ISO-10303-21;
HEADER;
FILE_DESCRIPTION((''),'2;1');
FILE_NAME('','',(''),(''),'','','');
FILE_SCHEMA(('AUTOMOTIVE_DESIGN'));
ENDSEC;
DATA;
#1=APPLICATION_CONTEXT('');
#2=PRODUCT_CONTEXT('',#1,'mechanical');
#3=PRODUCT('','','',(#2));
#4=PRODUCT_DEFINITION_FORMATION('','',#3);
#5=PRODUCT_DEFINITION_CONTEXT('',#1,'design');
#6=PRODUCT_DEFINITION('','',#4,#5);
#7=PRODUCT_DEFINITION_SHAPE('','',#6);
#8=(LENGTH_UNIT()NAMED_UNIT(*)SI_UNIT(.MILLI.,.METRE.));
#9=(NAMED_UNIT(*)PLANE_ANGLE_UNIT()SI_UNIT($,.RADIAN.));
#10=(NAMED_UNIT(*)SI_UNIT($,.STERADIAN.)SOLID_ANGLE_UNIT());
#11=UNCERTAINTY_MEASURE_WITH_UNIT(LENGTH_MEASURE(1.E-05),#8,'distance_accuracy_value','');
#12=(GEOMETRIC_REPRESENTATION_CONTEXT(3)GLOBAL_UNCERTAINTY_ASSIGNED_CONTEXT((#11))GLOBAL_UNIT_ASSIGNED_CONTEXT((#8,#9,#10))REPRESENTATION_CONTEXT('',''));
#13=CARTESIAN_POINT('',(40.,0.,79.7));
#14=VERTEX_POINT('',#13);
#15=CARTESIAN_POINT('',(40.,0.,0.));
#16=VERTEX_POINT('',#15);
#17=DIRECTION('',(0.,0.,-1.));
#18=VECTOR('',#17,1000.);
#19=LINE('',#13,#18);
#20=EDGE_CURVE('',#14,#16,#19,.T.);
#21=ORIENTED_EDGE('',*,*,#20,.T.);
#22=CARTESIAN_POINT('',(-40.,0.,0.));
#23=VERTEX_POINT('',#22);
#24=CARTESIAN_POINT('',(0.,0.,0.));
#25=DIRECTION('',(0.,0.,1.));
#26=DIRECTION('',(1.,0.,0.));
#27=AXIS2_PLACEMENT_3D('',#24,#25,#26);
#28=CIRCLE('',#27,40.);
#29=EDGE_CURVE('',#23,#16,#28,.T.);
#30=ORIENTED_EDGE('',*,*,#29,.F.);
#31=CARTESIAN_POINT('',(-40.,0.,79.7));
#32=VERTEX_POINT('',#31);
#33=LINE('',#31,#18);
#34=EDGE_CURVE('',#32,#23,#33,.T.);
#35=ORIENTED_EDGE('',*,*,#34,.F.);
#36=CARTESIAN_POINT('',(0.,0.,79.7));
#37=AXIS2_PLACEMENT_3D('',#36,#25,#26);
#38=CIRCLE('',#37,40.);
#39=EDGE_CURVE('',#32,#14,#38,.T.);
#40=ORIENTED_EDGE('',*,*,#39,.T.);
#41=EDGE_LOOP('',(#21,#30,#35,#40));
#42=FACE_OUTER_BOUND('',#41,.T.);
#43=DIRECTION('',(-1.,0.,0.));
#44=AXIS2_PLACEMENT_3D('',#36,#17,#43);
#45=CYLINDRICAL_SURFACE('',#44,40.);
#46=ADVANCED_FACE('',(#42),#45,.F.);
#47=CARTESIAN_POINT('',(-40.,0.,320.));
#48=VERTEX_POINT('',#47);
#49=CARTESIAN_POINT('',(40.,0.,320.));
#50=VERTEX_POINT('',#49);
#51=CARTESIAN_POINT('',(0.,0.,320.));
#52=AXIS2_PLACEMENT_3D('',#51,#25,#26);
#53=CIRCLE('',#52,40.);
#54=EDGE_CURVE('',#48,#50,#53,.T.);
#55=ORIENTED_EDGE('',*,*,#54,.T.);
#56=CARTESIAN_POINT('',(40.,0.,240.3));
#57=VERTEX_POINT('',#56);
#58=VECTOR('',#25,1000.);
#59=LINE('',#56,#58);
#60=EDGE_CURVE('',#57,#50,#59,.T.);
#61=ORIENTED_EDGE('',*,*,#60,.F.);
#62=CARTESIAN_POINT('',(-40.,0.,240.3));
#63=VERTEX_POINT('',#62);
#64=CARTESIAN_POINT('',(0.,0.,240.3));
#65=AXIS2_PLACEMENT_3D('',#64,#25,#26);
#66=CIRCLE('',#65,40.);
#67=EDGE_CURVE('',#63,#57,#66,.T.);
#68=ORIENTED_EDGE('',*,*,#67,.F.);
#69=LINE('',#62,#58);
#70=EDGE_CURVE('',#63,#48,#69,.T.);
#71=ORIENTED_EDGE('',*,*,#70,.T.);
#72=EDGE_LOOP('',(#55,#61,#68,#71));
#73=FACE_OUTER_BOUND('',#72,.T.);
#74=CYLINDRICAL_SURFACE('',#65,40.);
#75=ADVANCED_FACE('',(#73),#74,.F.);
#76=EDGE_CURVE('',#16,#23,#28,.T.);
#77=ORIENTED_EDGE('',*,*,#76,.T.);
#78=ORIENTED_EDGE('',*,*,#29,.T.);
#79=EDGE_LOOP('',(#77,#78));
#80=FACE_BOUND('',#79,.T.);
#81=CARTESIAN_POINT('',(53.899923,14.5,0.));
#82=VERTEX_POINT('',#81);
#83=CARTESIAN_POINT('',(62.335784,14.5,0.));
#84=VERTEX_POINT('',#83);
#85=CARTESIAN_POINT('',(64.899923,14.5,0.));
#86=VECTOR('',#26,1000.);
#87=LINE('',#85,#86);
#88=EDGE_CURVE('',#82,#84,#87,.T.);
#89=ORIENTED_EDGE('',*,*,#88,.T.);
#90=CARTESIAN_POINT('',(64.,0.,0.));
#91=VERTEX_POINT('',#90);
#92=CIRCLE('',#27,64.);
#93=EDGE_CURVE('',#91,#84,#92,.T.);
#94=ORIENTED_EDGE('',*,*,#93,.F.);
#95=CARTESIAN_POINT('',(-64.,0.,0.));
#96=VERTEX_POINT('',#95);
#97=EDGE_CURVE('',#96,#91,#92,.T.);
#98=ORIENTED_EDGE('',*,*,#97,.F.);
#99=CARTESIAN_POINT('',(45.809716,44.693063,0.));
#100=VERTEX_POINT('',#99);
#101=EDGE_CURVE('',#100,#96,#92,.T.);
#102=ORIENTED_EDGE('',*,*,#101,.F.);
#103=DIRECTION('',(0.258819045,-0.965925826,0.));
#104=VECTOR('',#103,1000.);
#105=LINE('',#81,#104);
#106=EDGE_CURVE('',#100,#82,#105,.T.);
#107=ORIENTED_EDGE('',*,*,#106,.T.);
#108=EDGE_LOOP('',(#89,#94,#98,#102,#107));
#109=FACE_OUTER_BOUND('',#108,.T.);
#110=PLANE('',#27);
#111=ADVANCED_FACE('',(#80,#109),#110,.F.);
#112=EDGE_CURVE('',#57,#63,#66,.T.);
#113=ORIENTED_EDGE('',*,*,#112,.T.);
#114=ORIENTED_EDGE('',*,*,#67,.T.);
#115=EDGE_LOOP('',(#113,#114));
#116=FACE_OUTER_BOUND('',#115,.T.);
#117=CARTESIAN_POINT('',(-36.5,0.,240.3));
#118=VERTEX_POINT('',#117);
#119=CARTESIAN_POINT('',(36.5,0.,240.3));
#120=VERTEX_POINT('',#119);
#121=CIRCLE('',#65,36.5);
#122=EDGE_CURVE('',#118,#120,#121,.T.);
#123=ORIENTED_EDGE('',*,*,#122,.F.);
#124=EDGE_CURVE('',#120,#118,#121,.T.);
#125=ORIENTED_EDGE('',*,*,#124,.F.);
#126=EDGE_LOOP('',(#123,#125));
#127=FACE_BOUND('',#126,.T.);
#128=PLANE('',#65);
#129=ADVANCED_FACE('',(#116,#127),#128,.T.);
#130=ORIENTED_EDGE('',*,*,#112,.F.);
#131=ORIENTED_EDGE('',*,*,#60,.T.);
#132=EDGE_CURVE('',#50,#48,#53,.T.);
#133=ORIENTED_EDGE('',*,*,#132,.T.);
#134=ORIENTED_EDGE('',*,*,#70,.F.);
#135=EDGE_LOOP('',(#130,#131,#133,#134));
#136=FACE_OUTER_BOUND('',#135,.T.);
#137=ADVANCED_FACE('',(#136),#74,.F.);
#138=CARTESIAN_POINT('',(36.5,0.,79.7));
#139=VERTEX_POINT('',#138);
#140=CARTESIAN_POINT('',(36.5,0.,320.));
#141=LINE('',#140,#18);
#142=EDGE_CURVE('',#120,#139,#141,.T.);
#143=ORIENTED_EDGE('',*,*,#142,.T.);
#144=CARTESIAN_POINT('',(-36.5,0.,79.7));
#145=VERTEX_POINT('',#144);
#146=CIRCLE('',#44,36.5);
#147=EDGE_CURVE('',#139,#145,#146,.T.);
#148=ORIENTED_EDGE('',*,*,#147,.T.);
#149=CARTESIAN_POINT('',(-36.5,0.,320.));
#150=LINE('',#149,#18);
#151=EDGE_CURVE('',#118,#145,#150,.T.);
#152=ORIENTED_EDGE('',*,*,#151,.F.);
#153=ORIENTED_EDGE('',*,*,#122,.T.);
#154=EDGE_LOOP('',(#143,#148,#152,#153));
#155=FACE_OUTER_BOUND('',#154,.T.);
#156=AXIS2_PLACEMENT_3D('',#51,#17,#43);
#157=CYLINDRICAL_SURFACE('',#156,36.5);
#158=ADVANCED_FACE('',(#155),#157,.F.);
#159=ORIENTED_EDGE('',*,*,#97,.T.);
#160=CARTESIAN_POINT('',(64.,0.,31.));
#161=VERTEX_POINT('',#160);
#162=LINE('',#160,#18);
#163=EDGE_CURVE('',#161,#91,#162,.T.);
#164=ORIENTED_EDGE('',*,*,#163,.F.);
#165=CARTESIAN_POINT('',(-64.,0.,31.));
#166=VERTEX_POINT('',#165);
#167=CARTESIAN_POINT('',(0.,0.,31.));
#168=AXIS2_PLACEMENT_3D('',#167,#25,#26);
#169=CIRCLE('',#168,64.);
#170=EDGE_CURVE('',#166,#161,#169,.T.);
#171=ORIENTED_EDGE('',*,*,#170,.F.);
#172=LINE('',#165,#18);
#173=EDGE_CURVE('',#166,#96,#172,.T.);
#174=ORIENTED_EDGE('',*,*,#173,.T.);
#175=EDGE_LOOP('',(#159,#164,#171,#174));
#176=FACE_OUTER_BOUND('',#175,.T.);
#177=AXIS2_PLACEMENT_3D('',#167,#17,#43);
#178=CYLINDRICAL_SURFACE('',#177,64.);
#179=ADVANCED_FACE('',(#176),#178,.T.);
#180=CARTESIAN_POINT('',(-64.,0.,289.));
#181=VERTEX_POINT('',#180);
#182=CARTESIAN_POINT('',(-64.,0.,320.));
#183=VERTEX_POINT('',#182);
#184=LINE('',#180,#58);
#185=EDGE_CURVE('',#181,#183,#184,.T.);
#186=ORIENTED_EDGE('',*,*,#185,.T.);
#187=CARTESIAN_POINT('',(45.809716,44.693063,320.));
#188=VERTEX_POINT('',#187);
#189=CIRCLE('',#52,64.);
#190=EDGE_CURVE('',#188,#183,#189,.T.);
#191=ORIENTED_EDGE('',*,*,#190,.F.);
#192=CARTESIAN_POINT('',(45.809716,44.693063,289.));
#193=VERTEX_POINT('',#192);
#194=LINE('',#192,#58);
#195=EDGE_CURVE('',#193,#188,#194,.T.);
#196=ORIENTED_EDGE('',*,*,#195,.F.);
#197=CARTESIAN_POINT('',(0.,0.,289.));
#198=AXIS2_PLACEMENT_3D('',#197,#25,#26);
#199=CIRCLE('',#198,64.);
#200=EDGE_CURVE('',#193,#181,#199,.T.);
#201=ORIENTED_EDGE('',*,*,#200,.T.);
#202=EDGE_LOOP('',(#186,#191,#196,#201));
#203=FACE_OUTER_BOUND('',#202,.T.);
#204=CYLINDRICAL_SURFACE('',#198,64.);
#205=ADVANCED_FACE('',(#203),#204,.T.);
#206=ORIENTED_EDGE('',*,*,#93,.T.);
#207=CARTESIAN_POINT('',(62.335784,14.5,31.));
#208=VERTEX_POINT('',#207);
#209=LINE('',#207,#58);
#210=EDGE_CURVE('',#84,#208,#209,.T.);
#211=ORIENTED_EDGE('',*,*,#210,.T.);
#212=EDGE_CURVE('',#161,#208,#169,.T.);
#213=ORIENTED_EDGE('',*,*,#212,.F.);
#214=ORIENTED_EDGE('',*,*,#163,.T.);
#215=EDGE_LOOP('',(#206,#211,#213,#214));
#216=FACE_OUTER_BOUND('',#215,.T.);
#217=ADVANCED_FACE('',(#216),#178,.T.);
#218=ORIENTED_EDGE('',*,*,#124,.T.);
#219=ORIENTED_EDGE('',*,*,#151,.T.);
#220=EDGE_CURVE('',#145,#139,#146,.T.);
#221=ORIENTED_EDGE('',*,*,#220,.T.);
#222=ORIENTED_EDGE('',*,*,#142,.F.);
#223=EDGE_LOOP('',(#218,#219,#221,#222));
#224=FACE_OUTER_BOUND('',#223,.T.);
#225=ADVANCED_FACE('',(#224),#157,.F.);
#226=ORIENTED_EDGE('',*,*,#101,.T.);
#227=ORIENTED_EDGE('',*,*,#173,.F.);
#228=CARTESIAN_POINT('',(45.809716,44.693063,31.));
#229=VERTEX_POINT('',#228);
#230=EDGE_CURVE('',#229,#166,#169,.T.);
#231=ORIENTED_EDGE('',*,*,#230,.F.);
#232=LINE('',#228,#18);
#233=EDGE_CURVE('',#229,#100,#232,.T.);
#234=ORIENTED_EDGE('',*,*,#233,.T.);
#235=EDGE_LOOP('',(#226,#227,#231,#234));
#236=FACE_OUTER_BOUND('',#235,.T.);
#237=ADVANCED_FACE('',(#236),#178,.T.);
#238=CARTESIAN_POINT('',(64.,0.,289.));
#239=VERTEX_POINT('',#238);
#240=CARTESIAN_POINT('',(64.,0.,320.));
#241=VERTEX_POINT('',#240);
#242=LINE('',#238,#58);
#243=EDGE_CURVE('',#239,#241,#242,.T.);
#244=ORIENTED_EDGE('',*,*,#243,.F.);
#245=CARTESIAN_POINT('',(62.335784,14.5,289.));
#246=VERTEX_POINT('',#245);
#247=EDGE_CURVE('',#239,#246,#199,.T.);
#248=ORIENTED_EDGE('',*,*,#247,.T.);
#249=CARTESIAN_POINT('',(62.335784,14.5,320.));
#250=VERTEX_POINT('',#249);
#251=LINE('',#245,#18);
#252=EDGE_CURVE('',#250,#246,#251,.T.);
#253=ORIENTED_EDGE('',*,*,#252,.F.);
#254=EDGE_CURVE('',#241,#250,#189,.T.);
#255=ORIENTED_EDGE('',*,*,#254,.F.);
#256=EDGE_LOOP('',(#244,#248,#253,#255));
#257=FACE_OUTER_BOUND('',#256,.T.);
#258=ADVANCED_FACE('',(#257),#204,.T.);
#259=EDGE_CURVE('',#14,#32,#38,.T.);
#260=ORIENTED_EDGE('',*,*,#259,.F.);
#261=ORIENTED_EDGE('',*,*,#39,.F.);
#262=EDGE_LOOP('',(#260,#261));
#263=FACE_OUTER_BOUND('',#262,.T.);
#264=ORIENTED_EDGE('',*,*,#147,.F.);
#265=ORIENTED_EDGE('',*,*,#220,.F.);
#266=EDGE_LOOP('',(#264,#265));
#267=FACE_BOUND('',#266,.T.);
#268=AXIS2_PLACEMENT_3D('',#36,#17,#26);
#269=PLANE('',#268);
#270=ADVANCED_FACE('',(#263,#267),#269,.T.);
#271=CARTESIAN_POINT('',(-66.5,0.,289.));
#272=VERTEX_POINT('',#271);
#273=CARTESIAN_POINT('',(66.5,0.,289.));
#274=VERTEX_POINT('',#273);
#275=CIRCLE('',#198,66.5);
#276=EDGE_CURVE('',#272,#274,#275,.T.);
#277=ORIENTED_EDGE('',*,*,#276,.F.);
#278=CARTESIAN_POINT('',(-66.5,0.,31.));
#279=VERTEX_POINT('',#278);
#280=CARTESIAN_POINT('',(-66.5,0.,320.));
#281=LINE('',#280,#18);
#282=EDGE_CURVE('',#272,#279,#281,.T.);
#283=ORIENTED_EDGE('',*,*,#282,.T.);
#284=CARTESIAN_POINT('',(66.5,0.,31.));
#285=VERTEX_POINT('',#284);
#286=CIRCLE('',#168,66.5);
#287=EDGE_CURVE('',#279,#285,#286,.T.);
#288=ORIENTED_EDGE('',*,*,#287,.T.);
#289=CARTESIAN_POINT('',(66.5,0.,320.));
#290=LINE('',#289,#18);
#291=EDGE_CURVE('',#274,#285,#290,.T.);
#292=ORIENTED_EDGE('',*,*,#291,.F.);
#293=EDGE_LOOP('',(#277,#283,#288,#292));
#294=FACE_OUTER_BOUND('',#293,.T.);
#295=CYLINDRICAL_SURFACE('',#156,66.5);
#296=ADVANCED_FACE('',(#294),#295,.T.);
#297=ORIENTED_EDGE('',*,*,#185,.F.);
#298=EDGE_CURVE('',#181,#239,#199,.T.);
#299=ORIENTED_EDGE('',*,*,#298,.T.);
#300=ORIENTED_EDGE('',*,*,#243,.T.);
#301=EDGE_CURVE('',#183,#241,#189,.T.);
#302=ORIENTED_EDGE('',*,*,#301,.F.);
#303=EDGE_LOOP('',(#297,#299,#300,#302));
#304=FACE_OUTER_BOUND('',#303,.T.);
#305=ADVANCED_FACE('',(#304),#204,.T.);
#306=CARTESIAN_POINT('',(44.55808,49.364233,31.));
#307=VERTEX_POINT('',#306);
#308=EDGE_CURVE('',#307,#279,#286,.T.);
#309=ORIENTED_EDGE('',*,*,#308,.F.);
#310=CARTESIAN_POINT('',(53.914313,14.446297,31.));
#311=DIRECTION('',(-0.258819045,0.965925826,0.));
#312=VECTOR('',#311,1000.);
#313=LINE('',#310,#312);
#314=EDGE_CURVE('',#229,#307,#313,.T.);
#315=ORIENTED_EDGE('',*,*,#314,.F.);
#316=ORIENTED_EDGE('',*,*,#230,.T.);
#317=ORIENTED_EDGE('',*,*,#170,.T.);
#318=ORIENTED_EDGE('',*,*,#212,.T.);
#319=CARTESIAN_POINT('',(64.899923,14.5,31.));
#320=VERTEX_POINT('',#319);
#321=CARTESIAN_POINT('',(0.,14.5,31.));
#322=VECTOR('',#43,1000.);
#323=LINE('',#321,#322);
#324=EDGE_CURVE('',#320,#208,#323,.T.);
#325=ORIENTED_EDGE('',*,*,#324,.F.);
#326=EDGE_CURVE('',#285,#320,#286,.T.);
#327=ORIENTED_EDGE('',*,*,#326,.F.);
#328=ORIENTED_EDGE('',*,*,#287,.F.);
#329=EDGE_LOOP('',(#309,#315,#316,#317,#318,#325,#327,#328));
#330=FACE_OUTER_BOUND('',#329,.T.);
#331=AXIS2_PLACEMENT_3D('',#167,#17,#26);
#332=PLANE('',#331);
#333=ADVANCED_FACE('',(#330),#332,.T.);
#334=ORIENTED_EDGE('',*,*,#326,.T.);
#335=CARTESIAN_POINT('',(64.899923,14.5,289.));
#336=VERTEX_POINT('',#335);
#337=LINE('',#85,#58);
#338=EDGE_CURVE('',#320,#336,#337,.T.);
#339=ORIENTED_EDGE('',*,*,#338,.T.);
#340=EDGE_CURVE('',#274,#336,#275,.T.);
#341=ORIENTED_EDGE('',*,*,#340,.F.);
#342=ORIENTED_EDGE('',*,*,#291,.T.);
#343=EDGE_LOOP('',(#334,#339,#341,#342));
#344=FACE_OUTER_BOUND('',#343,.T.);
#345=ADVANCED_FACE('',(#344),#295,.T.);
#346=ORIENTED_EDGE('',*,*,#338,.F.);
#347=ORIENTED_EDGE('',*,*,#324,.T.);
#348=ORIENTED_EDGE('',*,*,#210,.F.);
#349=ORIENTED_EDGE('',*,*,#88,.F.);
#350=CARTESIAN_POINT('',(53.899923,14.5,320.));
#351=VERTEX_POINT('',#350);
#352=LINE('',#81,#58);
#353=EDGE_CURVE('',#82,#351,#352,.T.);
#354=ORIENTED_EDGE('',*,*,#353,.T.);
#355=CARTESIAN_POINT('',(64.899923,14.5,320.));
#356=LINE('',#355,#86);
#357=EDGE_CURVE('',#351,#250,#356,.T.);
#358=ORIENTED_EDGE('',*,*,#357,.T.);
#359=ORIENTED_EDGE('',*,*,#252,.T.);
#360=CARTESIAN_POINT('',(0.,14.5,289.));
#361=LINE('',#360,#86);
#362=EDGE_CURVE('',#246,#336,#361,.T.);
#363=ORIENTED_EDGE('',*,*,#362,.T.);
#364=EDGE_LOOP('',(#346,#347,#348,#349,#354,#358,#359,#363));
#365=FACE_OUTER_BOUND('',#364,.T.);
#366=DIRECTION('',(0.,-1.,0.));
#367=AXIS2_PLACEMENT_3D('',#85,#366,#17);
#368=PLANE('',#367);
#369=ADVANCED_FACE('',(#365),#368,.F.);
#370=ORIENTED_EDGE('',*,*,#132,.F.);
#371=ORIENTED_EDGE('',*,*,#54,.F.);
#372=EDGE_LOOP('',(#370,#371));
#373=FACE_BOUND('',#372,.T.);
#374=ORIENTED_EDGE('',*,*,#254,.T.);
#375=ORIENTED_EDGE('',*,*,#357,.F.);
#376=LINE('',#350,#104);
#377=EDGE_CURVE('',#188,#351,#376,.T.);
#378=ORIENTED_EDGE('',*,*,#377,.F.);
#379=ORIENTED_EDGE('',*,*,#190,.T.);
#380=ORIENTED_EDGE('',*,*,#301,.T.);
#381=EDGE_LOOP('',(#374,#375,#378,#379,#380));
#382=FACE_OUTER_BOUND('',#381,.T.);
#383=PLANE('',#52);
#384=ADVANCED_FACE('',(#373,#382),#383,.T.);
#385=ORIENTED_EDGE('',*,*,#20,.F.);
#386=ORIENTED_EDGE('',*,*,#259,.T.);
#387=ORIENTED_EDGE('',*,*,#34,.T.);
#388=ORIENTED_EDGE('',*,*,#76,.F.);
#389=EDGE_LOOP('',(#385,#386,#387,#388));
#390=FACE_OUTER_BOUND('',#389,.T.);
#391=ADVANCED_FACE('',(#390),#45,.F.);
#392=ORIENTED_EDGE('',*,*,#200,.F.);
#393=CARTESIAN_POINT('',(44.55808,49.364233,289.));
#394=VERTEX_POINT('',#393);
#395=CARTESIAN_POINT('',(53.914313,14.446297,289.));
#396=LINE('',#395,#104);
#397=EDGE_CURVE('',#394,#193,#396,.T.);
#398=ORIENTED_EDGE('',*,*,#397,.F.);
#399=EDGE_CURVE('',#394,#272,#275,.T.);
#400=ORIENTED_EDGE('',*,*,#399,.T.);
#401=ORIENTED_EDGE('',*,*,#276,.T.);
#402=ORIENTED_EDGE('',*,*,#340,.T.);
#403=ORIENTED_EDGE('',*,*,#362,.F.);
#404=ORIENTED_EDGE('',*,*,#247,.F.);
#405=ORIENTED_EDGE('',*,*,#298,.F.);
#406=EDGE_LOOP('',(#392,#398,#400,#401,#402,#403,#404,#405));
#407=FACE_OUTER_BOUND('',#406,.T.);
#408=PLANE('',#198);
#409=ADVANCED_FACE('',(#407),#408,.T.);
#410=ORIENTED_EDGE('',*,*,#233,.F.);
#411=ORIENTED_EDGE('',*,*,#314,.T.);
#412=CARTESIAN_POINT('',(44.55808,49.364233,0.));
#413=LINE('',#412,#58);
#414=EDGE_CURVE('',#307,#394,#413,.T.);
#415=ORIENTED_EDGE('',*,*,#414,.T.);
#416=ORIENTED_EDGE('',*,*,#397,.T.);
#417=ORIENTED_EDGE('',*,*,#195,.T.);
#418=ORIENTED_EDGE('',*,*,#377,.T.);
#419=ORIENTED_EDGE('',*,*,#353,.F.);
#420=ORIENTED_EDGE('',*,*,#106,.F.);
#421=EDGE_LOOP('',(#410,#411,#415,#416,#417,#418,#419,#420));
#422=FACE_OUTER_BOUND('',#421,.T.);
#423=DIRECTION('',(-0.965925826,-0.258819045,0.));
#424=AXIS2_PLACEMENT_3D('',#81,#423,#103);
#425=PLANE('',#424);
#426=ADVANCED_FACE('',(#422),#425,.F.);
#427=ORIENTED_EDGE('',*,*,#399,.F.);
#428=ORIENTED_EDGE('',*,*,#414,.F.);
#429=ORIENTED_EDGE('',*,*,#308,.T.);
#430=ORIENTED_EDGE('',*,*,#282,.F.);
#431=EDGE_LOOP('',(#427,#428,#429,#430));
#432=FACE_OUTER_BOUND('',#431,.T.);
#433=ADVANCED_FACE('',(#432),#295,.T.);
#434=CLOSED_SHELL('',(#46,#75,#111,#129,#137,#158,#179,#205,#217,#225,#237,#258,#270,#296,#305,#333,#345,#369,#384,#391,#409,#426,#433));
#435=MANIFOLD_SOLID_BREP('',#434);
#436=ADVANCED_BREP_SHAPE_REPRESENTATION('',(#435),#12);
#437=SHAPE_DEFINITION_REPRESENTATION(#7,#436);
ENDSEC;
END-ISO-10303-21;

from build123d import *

# Parameters (mm, degrees)
SKETCH1_R           = 66.5
SKETCH1_R_2         = 36.5
BOSS_EXTRUDE1_DEPTH = 320
SKETCH3_R           = 40
CUT_EXTRUDE1_DEPTH  = 79.7
CUT_EXTRUDE2_START  = -31
SKETCH4_R           = 66.5
SKETCH4_R_2         = 64
CUT_EXTRUDE2_DEPTH  = 31
CUT_EXTRUDE3_DEPTH  = 334.533356653


with BuildPart() as part:
    # Sketch1 → Boss-Extrude1 (new body)
    with BuildSketch(Plane.XY):
        Circle(SKETCH1_R)
        Circle(SKETCH1_R_2, mode=Mode.SUBTRACT)
    extrude(amount=BOSS_EXTRUDE1_DEPTH)

    # Sketch3 → Cut-Extrude1 (cut)
    with BuildSketch(Plane.XY.offset(320)):
        Circle(SKETCH3_R)
    cut_extrude1 = extrude(amount=-CUT_EXTRUDE1_DEPTH, mode=Mode.SUBTRACT)

    # Sketch4 → Cut-Extrude2 (cut)
    with BuildSketch(Plane.XY.offset(320).offset(CUT_EXTRUDE2_START)):
        Circle(SKETCH4_R)
        Circle(SKETCH4_R_2, mode=Mode.SUBTRACT)
    cut_extrude2 = extrude(amount=CUT_EXTRUDE2_DEPTH, mode=Mode.SUBTRACT)

    # Mirror1: Cut-Extrude1, Cut-Extrude2 across plane
    add(cut_extrude1.mirror(Plane.XY.offset(160)), mode=Mode.SUBTRACT)
    add(cut_extrude2.mirror(Plane.XY.offset(160)), mode=Mode.SUBTRACT)

    # Sketch5 → Cut-Extrude3 (cut, through all)
    with BuildSketch(Plane.XY.offset(320)):
        with BuildLine():
            Line((64.899922958, 14.5), (53.899922958, 14.5))
            Line((53.899922958, 14.5), (44.558079818, 49.364233235))
            ThreePointArc((44.558079818, 49.364233235), (57.43816051, 33.512799305), (64.899922958, 14.5))
        make_face()
    extrude(amount=-CUT_EXTRUDE3_DEPTH, mode=Mode.SUBTRACT)


solid = part.part
